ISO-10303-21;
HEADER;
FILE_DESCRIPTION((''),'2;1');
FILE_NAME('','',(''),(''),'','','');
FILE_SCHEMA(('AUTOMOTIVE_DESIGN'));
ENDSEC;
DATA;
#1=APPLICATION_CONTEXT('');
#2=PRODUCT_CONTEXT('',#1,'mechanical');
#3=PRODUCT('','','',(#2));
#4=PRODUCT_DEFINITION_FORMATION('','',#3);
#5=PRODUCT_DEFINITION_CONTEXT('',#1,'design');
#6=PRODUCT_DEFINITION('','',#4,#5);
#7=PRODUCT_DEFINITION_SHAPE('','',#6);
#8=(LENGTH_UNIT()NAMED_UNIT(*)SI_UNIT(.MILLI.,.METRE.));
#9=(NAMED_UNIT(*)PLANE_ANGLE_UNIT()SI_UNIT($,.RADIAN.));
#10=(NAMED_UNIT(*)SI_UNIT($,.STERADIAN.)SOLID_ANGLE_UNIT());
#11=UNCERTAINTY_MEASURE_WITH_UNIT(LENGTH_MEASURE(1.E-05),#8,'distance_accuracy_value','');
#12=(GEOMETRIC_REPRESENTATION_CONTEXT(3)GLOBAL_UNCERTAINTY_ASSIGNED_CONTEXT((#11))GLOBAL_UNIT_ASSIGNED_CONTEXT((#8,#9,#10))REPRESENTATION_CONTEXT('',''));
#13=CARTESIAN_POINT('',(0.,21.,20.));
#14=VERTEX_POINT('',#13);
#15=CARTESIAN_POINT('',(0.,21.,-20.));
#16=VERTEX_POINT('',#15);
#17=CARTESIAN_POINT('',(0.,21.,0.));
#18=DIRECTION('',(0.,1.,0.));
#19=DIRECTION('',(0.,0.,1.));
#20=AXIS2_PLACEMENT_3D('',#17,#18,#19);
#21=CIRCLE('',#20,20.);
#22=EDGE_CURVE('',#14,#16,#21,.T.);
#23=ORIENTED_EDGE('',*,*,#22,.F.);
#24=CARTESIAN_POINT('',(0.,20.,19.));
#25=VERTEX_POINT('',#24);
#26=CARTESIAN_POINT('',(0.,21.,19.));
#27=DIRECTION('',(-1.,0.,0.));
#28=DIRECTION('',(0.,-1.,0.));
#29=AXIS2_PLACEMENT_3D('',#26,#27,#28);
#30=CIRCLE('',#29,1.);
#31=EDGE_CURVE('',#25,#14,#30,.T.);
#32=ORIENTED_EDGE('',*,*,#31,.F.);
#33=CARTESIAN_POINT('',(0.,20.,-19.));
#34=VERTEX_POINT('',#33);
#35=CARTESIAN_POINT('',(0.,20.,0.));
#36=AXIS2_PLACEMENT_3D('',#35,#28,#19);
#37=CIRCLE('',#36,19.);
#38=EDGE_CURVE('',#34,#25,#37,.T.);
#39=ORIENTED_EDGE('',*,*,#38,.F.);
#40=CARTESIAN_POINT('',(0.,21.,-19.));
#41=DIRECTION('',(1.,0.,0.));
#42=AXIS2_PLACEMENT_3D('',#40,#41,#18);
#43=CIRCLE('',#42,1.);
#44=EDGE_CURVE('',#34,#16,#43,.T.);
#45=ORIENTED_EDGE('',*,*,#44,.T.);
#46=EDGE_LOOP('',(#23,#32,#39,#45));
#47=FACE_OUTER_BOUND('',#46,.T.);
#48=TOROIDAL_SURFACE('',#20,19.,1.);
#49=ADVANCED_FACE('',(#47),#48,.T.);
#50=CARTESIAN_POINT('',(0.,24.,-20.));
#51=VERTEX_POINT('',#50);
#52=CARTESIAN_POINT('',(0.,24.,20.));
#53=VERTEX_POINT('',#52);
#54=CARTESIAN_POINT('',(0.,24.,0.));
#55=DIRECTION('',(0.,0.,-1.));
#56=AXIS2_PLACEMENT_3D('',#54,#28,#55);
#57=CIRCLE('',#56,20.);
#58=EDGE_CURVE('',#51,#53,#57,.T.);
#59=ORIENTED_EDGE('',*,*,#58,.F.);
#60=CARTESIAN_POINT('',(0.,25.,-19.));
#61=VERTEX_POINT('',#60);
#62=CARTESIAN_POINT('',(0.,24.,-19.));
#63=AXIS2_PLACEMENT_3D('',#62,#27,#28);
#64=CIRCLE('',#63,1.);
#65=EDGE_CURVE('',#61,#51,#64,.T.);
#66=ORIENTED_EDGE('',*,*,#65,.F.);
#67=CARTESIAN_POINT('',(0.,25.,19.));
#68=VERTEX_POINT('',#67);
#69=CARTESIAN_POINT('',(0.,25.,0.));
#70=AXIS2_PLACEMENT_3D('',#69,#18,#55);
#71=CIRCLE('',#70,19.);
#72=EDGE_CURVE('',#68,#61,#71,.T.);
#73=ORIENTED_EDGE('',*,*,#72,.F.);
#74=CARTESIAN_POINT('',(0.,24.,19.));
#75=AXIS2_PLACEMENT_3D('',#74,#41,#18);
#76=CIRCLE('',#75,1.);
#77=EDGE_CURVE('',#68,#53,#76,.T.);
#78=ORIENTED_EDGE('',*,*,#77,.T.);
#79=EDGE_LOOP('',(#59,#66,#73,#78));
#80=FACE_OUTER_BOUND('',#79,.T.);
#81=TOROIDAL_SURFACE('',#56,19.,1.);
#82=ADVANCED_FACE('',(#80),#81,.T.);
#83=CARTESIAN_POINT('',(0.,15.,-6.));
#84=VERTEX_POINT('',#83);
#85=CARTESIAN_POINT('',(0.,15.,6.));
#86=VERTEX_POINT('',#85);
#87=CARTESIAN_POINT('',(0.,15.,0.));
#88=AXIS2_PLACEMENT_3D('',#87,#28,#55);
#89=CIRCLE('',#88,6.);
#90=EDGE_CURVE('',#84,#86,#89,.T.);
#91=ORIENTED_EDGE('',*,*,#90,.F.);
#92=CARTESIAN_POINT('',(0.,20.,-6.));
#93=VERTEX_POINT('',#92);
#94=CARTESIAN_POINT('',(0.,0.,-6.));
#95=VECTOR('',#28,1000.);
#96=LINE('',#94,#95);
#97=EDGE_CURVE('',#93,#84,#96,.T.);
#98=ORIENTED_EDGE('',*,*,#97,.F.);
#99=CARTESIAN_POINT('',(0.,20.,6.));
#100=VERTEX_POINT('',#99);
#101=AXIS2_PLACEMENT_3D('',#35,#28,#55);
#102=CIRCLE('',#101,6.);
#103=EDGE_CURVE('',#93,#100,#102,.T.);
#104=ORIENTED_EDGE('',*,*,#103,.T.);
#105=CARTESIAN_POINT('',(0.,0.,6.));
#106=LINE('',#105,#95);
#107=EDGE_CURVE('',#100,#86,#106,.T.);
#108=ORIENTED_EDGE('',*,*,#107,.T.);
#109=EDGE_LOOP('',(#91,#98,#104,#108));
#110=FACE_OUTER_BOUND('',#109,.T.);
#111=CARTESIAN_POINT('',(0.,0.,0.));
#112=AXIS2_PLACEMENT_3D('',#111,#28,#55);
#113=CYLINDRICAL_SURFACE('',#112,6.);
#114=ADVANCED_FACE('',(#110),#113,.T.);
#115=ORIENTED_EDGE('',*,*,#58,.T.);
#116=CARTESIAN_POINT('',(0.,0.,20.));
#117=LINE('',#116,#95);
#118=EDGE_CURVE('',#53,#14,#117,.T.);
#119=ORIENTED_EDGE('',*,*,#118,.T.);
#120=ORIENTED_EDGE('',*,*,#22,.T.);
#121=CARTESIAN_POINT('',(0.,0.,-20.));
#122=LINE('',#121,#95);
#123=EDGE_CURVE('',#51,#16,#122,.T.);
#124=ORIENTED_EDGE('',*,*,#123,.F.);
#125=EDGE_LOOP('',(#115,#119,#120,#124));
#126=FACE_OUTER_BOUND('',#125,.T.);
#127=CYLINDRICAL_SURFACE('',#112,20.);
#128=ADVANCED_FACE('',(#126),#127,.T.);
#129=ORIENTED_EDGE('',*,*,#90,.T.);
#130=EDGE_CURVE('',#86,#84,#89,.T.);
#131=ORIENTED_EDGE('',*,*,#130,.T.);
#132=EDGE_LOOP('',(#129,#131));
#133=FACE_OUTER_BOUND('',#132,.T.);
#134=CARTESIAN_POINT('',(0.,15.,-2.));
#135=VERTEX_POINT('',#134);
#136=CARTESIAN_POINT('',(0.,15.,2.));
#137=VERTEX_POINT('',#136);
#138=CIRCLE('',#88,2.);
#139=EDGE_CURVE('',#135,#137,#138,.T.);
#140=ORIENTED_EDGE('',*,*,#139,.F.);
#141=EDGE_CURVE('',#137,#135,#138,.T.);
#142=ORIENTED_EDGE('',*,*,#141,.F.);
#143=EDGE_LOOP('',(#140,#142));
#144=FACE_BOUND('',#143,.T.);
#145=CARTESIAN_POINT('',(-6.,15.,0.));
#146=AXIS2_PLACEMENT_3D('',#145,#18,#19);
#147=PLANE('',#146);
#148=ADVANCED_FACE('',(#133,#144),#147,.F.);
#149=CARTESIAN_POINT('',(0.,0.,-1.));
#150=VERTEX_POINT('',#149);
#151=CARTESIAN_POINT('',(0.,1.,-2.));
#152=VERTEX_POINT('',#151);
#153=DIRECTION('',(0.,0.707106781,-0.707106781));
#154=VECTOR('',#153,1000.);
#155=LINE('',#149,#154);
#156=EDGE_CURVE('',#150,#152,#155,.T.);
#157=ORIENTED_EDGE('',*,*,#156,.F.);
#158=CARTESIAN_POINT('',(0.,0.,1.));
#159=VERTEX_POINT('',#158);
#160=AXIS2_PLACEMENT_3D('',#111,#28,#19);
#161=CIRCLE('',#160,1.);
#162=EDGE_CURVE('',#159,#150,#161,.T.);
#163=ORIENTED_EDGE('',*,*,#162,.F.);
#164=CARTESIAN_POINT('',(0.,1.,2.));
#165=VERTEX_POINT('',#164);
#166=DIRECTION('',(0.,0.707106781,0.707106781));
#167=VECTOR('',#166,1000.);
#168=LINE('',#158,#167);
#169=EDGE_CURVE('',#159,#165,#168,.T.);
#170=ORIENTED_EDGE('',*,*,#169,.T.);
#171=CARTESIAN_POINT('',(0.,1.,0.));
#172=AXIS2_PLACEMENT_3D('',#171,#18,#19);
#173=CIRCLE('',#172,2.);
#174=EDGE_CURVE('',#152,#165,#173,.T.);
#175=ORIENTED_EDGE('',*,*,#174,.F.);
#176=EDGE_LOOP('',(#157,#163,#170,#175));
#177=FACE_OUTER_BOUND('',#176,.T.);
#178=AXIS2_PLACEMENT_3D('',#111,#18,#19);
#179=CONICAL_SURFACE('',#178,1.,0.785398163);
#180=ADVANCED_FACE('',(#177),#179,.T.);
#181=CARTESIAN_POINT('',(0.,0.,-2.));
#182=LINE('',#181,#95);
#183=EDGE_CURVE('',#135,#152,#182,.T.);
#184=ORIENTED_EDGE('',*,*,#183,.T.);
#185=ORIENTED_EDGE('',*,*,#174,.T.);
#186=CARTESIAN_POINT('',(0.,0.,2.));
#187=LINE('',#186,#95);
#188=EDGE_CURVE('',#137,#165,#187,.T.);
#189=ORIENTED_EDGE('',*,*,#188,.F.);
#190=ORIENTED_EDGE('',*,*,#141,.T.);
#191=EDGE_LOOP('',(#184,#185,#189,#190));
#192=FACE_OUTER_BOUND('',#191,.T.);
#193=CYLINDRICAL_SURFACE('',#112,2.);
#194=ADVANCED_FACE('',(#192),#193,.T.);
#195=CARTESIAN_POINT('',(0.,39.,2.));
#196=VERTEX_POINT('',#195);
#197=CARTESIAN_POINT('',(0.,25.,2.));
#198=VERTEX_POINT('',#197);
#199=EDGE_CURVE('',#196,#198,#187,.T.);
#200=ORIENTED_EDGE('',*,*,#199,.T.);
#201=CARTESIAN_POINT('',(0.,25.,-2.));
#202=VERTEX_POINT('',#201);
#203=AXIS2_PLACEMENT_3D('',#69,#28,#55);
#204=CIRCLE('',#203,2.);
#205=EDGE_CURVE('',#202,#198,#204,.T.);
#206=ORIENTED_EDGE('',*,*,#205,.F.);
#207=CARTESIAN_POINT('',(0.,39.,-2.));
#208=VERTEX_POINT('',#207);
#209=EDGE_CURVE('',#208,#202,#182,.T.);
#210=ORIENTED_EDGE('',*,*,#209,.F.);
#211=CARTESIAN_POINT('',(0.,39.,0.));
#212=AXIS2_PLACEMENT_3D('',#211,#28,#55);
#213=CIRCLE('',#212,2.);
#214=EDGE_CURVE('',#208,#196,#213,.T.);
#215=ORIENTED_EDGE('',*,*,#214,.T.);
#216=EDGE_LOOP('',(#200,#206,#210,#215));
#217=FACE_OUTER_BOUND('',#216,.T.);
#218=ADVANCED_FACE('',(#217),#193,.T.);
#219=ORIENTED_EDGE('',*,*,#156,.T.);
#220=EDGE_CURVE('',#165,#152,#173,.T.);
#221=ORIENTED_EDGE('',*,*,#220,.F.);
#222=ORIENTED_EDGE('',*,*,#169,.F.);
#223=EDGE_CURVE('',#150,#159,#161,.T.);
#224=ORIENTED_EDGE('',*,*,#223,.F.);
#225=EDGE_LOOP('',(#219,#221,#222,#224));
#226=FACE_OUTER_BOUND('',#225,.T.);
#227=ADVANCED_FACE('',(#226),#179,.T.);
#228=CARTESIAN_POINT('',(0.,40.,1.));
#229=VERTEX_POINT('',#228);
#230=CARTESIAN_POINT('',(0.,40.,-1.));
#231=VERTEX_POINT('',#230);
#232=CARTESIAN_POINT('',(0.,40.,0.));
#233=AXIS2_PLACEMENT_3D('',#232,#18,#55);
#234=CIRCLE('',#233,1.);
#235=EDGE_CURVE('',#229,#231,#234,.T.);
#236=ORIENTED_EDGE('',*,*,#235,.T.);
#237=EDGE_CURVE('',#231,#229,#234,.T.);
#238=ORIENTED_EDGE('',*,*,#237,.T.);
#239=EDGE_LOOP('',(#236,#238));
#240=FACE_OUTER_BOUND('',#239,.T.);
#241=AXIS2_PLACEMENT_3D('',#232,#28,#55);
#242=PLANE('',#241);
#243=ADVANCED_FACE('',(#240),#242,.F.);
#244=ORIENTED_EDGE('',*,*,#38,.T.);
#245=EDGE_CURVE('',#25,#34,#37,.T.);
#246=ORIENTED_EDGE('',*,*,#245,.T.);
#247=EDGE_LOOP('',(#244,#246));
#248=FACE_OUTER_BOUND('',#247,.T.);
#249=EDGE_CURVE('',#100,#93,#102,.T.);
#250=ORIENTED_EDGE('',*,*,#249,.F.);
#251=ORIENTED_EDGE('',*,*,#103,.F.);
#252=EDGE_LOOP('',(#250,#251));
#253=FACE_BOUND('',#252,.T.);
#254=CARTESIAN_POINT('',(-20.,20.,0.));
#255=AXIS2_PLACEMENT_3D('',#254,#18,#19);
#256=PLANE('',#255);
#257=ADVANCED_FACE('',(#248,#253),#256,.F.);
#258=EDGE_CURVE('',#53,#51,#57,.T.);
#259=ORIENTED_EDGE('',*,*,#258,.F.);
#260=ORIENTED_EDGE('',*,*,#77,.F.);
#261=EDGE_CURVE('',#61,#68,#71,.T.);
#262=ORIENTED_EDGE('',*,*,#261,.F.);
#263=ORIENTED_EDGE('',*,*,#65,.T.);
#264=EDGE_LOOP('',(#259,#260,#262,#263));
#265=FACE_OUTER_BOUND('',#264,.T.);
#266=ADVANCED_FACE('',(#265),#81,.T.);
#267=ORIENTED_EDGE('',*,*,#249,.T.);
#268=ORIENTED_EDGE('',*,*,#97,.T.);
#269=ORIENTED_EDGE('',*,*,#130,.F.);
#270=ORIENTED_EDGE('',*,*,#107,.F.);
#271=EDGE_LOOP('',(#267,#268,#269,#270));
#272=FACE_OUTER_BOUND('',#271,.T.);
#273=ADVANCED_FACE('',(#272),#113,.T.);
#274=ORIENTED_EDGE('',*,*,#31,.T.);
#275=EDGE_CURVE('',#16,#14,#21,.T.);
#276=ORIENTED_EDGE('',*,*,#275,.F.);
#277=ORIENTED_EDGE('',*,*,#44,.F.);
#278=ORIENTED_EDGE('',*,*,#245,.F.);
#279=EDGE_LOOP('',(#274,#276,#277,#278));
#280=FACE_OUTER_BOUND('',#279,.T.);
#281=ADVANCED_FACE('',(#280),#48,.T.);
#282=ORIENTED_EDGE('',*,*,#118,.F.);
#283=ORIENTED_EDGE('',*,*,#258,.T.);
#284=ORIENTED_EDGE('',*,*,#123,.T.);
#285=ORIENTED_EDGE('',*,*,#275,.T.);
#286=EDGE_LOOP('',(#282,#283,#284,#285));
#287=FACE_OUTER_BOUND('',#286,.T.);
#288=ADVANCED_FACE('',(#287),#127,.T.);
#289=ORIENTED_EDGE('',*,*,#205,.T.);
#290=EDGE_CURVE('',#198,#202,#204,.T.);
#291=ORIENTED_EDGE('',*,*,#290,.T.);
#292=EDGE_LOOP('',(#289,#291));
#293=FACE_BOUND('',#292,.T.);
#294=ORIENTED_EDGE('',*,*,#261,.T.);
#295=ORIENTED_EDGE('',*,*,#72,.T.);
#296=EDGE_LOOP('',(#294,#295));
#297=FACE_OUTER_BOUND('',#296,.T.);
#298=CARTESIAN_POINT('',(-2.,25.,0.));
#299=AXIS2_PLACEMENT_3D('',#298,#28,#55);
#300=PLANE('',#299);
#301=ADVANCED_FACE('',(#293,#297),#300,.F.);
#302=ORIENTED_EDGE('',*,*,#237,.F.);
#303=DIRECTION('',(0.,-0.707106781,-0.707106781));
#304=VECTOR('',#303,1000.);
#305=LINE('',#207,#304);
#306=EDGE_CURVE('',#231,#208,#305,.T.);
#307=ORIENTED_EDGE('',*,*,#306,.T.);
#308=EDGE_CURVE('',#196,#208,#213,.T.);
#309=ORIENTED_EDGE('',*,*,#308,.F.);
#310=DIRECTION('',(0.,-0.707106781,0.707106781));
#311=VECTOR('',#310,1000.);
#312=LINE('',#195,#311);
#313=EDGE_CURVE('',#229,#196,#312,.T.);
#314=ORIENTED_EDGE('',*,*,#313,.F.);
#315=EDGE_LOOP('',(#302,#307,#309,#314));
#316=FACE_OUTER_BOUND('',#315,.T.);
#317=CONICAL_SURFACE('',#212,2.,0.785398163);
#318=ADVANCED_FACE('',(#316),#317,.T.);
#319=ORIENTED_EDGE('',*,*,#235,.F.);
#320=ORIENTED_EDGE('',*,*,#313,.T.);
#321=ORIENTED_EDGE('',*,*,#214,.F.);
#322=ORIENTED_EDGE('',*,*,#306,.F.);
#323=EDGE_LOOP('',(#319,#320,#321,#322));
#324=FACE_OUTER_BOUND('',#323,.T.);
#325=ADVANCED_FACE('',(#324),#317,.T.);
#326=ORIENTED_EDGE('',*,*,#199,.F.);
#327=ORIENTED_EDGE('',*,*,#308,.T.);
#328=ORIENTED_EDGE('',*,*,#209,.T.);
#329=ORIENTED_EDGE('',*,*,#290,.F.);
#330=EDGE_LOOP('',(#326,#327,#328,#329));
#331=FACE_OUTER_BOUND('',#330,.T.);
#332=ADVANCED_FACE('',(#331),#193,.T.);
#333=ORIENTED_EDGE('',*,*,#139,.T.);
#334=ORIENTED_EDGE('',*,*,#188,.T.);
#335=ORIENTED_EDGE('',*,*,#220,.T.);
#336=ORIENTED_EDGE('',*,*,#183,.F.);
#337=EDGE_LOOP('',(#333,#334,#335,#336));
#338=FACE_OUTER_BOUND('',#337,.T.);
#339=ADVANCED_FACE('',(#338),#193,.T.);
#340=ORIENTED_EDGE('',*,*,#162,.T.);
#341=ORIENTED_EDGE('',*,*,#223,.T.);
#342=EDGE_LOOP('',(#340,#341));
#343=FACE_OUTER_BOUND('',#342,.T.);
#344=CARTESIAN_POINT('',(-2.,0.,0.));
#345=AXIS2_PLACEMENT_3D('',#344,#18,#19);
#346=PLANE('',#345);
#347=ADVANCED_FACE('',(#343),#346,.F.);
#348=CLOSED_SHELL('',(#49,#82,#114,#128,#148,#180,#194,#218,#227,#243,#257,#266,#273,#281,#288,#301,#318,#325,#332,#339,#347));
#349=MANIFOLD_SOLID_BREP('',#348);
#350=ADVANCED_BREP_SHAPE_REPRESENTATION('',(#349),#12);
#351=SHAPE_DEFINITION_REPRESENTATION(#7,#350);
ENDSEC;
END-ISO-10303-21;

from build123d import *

# Parameters (mm, degrees)
CHAMFER1_SIZE = 1
FILLET1_R     = 1


with BuildPart() as part:
    # Sketch1 → Revolve1 (revolve)
    with BuildSketch(Plane.XY, mode=Mode.PRIVATE) as revolve1_sk:
        Polygon((0, 40), (-2, 40), (-2, 25), (-20, 25), (-20, 20), (-6, 20), (-6, 15), (-2, 15), (-2, 0), (0, 0), align=None)
    revolve(revolve1_sk.sketch.rotate(Axis((0, 0, 0), (0, 1, 0)), 270), axis=Axis((0, 0, 0), (0, 1, 0)))

    # Chamfer1
    chamfer1_edges = [part.edges().sort_by_distance(p)[0] for p in [
        (0, 40, 2),
        (0, 0, 2),
    ]]
    chamfer(chamfer1_edges, length=CHAMFER1_SIZE)

    # Fillet1
    fillet1_edges = [part.edges().sort_by_distance(p)[0] for p in [
        (0, 20, 20),
        (0, 25, 20),
    ]]
    fillet(fillet1_edges, radius=FILLET1_R)


solid = part.part
